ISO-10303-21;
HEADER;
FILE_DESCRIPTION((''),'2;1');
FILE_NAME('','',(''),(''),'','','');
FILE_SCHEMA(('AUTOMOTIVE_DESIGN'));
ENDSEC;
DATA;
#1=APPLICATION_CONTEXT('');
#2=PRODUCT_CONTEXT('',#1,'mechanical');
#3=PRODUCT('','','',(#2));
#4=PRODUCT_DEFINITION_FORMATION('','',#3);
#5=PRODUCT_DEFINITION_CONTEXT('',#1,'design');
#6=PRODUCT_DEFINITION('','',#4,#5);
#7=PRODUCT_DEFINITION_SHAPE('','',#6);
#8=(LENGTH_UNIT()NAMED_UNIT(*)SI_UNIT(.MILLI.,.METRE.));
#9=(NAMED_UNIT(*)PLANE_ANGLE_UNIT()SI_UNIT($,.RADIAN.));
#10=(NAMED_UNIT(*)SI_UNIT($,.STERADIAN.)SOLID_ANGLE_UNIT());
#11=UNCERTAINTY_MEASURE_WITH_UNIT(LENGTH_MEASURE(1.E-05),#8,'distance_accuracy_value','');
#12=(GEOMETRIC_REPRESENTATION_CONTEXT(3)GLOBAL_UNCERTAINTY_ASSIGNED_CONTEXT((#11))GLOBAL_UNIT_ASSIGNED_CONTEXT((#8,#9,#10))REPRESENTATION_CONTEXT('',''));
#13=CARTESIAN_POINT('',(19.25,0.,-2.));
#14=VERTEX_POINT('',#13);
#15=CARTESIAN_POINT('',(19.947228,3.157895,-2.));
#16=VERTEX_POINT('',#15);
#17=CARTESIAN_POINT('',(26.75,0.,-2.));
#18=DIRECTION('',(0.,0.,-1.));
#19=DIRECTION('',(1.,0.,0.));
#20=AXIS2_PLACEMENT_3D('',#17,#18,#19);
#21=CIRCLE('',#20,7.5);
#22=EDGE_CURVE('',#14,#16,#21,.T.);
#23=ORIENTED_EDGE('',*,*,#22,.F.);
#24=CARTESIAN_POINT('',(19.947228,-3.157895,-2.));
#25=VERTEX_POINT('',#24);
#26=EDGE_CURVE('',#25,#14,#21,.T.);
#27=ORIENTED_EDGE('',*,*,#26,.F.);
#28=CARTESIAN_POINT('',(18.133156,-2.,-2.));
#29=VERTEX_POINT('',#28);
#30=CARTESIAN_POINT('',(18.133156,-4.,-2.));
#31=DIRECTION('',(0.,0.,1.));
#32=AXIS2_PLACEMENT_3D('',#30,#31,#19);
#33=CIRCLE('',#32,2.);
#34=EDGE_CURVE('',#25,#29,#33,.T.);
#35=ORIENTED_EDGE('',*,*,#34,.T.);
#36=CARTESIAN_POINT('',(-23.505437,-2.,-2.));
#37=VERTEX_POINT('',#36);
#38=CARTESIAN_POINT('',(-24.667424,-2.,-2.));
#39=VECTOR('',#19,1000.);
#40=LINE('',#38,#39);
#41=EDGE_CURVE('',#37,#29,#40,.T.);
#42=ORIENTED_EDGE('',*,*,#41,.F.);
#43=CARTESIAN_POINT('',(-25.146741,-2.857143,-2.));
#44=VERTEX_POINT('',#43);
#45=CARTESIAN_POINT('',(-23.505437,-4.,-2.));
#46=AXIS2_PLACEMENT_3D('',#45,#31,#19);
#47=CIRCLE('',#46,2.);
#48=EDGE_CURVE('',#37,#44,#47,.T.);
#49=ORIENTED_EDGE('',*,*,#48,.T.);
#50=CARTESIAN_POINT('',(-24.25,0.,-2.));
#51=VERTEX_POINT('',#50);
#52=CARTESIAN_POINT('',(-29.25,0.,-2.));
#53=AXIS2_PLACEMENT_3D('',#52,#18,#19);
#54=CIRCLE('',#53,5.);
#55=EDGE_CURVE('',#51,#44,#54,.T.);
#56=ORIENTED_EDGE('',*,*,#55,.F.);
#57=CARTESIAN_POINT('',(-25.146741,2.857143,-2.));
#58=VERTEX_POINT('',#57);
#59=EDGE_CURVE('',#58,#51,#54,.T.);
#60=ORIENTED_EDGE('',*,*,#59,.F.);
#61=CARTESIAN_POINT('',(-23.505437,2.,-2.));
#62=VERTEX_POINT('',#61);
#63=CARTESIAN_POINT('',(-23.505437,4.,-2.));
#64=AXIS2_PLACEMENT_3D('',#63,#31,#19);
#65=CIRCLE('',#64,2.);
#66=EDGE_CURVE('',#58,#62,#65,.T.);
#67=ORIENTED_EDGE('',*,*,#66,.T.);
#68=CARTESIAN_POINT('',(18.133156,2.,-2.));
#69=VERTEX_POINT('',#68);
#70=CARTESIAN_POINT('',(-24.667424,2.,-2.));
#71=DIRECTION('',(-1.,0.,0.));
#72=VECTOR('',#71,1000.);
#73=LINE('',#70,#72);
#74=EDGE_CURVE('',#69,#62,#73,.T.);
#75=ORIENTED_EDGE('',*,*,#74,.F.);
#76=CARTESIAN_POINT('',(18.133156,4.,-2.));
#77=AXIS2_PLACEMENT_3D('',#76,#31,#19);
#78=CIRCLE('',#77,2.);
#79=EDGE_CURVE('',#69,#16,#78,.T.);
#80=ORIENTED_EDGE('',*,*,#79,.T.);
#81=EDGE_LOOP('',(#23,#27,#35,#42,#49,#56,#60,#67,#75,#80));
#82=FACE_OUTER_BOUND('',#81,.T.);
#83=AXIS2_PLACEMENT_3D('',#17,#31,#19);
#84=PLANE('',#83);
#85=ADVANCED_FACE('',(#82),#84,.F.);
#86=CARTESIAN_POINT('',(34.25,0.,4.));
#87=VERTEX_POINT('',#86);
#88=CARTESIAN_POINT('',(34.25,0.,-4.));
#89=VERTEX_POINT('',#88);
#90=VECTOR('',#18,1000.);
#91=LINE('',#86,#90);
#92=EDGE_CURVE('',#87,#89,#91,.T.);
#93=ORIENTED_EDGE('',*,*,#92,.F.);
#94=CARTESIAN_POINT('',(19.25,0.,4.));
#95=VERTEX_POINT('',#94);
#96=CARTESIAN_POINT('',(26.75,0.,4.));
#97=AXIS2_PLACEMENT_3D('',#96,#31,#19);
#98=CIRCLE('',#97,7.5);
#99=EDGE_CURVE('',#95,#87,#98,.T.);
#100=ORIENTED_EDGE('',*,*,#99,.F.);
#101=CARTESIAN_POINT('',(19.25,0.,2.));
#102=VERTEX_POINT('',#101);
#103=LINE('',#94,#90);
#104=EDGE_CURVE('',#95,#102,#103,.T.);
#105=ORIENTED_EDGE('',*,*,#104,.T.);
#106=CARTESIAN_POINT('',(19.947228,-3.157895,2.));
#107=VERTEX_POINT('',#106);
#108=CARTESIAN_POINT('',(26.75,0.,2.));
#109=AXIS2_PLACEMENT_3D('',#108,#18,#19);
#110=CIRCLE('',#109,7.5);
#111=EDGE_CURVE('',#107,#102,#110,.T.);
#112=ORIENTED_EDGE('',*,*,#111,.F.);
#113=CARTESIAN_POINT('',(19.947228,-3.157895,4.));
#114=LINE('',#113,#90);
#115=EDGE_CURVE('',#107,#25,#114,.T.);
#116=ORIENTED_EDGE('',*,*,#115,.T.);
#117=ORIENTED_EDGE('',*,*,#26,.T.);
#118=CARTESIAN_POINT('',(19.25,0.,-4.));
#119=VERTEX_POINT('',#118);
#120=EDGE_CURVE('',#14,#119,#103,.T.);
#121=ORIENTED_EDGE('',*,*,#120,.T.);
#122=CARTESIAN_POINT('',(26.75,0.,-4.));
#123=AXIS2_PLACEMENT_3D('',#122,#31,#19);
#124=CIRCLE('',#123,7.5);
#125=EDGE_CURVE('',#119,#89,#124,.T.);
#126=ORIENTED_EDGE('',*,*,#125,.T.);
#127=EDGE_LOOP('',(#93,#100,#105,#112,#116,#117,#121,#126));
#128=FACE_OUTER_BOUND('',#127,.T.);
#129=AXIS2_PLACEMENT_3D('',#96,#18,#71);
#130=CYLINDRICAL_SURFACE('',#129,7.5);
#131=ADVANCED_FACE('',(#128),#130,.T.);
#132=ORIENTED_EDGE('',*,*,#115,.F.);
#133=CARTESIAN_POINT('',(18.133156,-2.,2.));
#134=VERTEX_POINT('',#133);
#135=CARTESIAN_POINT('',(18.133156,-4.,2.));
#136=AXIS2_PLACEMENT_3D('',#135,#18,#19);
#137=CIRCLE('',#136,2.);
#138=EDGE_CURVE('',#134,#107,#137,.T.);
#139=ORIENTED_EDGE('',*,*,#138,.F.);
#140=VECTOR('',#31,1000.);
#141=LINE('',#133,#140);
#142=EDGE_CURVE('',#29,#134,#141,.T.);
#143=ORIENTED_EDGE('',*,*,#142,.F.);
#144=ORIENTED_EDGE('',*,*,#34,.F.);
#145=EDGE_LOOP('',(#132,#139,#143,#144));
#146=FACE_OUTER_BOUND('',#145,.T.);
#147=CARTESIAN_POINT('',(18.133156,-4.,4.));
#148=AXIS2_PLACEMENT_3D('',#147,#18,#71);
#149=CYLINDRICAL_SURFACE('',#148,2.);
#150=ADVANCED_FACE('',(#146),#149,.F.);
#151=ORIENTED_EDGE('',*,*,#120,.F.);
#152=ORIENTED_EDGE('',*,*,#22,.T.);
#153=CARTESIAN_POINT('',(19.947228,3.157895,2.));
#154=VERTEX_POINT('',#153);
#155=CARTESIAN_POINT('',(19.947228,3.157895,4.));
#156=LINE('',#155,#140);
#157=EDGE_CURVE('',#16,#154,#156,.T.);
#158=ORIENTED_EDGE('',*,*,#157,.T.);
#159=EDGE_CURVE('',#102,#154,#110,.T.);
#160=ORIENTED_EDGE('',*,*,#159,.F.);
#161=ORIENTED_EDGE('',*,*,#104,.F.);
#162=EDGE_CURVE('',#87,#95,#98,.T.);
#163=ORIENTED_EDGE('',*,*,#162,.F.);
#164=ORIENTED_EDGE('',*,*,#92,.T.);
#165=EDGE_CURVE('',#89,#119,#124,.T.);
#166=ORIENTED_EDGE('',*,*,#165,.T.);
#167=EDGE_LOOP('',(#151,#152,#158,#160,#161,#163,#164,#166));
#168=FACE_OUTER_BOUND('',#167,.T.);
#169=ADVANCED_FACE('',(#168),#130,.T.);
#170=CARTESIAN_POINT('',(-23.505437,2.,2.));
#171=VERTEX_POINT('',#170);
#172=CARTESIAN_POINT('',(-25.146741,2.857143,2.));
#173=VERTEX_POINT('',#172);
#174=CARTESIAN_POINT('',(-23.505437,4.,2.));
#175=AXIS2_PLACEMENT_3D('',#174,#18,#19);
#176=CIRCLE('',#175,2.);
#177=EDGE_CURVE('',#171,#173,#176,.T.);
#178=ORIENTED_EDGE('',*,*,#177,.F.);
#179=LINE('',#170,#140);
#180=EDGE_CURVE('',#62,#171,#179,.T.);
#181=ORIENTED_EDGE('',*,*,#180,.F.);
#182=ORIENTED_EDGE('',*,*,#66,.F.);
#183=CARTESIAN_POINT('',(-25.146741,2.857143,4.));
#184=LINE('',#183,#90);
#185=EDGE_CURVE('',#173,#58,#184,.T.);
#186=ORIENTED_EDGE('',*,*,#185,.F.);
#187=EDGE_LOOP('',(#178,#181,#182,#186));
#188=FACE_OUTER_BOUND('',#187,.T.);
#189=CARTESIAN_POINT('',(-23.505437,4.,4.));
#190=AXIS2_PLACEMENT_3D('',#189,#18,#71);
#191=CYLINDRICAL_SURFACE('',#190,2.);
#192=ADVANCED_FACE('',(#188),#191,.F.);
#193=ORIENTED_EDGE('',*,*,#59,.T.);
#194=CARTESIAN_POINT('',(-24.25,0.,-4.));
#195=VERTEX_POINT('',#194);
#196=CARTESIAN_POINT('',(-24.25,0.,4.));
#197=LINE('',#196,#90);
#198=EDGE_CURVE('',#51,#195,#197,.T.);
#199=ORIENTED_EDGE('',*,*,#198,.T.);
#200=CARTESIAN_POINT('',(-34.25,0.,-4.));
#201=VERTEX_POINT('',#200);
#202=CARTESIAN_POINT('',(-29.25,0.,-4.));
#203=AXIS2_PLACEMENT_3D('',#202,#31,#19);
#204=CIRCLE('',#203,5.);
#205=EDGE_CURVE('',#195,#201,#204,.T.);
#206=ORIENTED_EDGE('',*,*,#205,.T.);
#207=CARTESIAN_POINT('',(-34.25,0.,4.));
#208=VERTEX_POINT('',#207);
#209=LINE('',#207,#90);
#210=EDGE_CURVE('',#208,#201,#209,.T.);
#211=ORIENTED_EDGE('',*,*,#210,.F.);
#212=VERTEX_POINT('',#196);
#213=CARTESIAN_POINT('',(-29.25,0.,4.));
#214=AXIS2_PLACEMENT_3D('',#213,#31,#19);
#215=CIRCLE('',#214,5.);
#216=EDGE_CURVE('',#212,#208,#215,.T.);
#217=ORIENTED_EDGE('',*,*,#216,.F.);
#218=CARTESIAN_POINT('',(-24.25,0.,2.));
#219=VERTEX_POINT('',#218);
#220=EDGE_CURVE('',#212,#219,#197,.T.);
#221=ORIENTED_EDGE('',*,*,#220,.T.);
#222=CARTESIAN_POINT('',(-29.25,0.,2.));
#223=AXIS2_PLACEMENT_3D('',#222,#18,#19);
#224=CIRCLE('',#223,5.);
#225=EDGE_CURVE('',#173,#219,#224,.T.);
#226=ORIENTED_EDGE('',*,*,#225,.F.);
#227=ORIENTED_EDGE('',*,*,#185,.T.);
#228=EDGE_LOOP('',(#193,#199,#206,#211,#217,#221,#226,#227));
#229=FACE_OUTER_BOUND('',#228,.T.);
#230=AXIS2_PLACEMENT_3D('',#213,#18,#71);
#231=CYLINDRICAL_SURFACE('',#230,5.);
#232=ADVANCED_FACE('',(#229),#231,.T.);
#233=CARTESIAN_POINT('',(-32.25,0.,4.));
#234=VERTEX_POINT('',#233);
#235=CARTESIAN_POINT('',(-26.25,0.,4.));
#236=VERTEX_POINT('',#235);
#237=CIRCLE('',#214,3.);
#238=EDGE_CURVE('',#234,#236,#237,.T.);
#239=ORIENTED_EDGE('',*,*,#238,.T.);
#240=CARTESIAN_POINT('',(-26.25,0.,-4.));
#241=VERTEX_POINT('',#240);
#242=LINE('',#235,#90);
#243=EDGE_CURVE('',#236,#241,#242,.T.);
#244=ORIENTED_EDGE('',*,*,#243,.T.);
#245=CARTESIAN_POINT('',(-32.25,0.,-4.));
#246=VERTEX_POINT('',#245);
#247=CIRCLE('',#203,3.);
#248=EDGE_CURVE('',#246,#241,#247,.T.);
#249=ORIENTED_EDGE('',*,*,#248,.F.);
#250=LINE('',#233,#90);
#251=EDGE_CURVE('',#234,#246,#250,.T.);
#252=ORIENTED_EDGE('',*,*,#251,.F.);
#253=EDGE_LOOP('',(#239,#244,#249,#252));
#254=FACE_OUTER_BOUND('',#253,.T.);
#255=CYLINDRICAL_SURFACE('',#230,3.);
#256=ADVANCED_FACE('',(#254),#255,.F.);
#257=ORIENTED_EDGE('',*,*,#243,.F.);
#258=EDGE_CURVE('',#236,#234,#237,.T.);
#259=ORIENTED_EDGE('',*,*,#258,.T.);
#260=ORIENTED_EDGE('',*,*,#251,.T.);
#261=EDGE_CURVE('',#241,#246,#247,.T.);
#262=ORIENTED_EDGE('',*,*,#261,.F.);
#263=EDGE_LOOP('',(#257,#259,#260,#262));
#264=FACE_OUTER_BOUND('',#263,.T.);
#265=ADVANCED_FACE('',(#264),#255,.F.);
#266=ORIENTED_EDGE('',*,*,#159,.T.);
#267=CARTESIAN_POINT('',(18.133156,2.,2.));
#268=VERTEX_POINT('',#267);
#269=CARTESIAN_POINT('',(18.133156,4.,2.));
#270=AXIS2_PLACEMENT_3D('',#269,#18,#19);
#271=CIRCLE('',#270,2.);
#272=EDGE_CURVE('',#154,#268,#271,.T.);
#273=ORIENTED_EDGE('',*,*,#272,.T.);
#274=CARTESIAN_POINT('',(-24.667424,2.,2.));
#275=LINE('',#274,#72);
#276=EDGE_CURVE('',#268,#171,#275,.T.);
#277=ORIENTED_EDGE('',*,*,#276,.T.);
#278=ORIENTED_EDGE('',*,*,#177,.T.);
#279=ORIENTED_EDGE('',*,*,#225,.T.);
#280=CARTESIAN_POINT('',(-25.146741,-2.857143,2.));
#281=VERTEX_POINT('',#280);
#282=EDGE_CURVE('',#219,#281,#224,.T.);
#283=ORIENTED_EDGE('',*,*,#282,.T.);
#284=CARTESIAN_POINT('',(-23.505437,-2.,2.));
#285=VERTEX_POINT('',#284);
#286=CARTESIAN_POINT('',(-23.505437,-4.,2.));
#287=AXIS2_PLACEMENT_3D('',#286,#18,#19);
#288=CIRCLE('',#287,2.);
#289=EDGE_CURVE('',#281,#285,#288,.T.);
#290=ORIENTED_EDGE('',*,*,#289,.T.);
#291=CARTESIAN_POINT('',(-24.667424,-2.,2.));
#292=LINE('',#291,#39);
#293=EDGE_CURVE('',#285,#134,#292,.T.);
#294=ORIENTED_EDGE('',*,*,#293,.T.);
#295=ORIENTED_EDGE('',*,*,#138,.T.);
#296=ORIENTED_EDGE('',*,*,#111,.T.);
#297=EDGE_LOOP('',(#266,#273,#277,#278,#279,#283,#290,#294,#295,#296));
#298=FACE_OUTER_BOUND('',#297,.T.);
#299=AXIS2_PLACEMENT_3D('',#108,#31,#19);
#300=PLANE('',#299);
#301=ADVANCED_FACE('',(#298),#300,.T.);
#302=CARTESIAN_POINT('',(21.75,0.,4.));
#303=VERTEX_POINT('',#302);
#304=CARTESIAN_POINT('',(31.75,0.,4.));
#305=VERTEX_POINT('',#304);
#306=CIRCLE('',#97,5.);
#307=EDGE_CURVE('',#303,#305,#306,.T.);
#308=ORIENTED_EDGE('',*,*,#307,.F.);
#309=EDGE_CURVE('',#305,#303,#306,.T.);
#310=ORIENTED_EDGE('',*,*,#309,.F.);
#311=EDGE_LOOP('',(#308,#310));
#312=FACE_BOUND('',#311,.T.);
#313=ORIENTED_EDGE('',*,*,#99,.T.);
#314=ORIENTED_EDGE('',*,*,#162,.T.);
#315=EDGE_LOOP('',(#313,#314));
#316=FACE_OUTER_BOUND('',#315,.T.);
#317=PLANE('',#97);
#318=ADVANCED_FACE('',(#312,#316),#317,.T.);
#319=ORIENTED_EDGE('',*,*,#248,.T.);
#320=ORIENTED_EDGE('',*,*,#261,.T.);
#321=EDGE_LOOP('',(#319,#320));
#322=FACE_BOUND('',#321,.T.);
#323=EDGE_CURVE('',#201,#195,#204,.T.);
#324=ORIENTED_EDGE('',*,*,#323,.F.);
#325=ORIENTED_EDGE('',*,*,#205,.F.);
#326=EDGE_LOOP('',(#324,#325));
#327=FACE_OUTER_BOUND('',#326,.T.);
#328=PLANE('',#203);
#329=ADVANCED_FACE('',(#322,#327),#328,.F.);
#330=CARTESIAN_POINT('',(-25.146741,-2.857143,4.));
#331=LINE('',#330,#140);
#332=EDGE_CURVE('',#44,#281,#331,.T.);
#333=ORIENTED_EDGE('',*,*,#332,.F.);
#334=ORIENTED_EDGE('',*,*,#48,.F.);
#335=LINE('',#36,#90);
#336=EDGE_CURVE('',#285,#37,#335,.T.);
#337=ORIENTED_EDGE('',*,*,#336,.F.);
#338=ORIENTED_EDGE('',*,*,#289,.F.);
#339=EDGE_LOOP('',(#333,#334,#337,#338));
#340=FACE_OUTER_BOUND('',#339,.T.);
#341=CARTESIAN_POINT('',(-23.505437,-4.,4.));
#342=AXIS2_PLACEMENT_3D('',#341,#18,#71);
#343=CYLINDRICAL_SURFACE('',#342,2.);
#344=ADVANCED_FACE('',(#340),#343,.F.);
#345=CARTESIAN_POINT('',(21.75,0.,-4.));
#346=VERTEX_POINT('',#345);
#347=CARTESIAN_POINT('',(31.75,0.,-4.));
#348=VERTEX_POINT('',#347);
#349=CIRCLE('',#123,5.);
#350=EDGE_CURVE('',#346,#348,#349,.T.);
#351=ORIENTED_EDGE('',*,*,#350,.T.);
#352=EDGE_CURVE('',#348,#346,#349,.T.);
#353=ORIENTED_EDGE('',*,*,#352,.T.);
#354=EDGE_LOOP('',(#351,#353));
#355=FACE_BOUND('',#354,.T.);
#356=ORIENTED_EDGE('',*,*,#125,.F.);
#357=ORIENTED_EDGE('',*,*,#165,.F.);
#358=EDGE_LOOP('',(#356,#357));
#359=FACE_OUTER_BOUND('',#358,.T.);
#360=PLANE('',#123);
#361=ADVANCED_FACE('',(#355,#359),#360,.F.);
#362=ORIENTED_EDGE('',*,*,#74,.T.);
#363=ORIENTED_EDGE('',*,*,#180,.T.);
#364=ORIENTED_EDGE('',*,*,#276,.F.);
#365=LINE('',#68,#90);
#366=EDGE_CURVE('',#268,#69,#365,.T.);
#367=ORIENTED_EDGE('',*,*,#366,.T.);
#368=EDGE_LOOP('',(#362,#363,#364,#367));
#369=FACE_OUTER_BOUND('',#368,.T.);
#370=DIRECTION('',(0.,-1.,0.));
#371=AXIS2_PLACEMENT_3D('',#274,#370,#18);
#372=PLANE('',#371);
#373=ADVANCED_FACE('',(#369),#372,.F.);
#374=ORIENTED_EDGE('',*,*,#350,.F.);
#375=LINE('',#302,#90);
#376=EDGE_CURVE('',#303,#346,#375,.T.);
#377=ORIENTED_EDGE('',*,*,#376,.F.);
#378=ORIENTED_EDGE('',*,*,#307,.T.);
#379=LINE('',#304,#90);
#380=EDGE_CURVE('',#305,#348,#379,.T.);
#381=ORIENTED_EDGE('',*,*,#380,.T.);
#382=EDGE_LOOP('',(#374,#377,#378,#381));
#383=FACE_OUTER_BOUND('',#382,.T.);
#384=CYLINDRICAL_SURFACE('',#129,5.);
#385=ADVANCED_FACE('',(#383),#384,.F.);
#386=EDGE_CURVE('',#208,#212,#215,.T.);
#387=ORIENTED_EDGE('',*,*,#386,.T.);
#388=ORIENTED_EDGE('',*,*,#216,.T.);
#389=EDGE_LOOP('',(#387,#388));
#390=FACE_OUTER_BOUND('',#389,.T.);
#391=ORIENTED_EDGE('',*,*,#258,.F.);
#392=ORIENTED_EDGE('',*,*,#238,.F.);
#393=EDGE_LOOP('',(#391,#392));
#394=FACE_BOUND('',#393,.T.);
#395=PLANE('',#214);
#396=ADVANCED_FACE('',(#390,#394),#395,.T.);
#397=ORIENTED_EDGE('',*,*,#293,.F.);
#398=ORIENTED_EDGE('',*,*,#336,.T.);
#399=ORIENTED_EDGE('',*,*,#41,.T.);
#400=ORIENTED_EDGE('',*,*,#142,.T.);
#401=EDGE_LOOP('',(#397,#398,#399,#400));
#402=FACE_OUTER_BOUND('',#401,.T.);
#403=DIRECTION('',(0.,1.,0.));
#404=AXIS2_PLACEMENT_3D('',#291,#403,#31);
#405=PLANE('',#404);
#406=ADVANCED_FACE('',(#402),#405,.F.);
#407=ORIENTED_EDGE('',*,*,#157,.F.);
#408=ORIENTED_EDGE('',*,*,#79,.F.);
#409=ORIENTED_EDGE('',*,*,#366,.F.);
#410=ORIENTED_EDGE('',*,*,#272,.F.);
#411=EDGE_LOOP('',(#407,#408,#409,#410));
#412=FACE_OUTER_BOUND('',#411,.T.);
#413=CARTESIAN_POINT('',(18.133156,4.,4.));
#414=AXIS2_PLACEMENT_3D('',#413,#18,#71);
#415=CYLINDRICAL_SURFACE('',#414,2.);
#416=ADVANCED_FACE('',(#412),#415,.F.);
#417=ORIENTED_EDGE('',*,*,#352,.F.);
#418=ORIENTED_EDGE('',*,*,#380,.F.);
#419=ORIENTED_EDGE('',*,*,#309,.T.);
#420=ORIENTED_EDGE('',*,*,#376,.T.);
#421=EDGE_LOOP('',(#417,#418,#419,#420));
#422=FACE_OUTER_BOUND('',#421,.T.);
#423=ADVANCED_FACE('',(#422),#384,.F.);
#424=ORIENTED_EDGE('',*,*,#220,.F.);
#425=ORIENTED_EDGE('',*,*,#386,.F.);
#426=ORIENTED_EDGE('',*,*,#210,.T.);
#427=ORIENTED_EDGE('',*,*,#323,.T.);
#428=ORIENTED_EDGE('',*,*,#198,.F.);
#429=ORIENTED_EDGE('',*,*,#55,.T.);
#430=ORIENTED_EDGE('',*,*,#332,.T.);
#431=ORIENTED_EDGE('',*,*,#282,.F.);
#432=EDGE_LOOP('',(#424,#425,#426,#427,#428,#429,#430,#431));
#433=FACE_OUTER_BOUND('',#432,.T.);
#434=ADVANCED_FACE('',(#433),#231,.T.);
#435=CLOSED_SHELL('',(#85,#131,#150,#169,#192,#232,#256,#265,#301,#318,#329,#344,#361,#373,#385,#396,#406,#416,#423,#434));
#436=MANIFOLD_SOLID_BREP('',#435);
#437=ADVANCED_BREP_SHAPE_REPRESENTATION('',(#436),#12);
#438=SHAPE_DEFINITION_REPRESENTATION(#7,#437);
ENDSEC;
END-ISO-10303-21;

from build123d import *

# Parameters (mm, degrees)
ROD_PROFILE_SKETCH_R         = 5
ROD_PROFILE_SKETCH_R_2       = 3
ROD_BODY_EXTRUDE_8MM_DEPTH   = 4
ROD_PROFILE_SKETCH_R_3       = 7.5
ROD_BODY_EXTRUDE_8MM_2_DEPTH = 4
SHANK_BOSS_4MM_DEPTH         = 2
SHANK_FILLET_R2_R            = 2


with BuildPart() as part:
    # Rod Profile Sketch → Rod Body Extrude 8mm (new, symmetric)
    with BuildSketch(Plane.XY):
        with Locations((-29.25, 0)):
            Circle(ROD_PROFILE_SKETCH_R)
        with Locations((-29.25, 0)):
            Circle(ROD_PROFILE_SKETCH_R_2, mode=Mode.SUBTRACT)
    extrude(amount=ROD_BODY_EXTRUDE_8MM_DEPTH, both=True)



with BuildPart() as body_2:
    # Rod Profile Sketch → Rod Body Extrude 8mm 2 (new, symmetric)
    with BuildSketch(Plane.XY):
        with Locations((26.75, 0)):
            Circle(ROD_PROFILE_SKETCH_R_3)
        with Locations((26.75, 0)):
            Circle(ROD_PROFILE_SKETCH_R, mode=Mode.SUBTRACT)
    extrude(amount=ROD_BODY_EXTRUDE_8MM_2_DEPTH, both=True)


with BuildPart() as part_1:
    add(part.part)

    add(body_2.part)  # Shank Boss 4mm merges body 2
    # Shank Boss Sketch → Shank Boss 4mm (add, symmetric)
    with BuildSketch(Plane.XY):
        with BuildLine():
            Line((-24.667424305, 2), (19.521583853, 2))
            ThreePointArc((19.521583853, 2), (19.25, 0), (19.521583853, -2))
            Line((19.521583853, -2), (-24.667424305, -2))
            ThreePointArc((-24.667424305, -2), (-24.25, 0), (-24.667424305, 2))
        make_face()
    extrude(amount=SHANK_BOSS_4MM_DEPTH, both=True)

    # Shank Fillet R2
    shank_fillet_r2_edges = [part_1.edges().sort_by_distance(p)[0] for p in [
        (19.521583853, -2, 0),
        (19.521583853, 2, 0),
        (-24.667424305, 2, 0),
        (-24.667424305, -2, 0),
    ]]
    fillet(shank_fillet_r2_edges, radius=SHANK_FILLET_R2_R)


solid = part_1.part
